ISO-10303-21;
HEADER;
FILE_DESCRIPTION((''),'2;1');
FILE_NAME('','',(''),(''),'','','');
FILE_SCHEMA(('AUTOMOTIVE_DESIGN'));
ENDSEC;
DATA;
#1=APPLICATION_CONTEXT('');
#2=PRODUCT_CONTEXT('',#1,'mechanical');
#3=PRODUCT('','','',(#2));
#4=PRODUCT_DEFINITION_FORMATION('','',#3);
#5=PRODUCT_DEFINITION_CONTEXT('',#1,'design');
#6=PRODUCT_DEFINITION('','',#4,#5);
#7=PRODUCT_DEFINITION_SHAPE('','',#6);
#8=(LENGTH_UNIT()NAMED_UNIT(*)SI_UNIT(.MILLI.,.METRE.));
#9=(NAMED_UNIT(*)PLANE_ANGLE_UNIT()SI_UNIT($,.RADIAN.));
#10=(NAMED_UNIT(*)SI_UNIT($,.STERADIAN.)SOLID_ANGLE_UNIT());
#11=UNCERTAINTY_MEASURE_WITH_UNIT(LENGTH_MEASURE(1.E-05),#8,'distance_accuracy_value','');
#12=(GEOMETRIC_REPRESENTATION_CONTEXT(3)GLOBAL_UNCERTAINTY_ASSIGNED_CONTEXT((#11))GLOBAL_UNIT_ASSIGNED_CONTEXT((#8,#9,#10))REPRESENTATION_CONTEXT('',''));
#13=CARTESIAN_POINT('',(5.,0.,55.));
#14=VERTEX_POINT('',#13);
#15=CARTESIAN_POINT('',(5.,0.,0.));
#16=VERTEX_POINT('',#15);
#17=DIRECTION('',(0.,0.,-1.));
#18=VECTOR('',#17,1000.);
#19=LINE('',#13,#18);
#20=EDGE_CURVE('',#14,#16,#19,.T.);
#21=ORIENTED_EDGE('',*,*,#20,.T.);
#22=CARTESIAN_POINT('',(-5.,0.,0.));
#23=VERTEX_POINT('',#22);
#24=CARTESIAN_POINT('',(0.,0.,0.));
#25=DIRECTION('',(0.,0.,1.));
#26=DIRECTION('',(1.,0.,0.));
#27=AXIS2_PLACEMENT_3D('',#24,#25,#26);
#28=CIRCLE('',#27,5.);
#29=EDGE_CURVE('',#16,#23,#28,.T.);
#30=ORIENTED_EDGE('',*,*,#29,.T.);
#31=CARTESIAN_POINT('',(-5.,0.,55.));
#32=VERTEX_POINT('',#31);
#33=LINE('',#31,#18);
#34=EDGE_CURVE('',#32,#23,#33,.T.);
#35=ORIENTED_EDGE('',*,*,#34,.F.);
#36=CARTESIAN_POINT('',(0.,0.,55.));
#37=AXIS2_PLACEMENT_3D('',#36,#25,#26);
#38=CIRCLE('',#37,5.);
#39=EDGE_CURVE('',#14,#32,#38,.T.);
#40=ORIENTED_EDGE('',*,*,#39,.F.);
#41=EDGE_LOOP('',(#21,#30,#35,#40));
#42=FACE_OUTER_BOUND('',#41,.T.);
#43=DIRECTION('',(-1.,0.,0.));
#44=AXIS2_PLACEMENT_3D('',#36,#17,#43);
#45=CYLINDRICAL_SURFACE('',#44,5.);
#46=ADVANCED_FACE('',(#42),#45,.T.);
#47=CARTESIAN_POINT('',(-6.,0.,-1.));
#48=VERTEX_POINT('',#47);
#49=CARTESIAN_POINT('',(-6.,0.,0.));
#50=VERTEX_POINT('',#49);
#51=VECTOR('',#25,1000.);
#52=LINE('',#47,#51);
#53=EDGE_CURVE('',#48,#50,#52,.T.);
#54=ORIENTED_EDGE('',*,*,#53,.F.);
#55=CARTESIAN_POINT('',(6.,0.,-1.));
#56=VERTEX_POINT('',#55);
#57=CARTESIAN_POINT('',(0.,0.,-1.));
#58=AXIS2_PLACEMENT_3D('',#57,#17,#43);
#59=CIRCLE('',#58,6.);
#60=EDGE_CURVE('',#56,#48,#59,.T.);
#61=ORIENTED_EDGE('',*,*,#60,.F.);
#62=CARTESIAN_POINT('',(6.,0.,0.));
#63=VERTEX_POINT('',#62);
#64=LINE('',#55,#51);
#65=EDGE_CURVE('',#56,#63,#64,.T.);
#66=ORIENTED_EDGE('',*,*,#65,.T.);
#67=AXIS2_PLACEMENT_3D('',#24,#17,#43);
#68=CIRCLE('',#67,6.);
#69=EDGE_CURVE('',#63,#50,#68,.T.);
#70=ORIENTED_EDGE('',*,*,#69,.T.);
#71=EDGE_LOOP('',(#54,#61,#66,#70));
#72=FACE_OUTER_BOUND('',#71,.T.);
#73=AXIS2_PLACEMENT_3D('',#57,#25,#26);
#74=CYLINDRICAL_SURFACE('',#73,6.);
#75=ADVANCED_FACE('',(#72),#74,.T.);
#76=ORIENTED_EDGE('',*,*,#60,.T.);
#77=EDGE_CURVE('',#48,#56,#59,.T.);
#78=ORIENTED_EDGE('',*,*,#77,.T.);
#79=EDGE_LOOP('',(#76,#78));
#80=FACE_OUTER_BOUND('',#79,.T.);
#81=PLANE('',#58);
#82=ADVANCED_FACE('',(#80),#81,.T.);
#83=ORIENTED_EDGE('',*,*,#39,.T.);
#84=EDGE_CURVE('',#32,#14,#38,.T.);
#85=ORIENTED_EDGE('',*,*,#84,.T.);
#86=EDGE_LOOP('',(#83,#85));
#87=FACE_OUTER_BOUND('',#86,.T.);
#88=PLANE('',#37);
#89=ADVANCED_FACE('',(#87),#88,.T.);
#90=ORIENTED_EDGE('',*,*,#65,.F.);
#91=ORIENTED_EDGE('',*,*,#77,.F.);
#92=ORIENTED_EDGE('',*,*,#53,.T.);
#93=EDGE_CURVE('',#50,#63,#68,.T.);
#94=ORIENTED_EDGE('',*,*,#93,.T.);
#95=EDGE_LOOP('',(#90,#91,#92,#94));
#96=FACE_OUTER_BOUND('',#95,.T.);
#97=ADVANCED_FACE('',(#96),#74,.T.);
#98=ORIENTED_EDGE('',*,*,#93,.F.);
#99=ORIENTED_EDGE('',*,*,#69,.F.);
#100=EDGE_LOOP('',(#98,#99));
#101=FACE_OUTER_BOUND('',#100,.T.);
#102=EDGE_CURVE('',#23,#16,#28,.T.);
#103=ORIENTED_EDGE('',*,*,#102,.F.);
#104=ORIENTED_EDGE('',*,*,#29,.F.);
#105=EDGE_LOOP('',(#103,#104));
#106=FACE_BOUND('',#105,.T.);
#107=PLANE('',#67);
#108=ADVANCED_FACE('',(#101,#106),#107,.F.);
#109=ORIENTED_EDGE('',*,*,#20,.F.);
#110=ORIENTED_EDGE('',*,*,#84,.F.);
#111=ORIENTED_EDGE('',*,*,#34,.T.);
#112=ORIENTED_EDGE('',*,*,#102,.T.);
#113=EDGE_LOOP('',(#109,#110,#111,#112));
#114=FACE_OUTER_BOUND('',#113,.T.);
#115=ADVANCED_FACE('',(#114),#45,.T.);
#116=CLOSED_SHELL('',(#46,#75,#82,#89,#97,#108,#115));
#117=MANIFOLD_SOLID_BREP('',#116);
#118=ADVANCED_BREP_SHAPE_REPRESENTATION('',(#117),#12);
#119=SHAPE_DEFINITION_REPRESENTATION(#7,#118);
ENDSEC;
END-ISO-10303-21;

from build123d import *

# Parameters (mm, degrees)
SKETCH_1_R      = 5
EXTRUDE_1_DEPTH = 55
SKETCH_2_R      = 6
EXTRUDE_2_DEPTH = 1


with BuildPart() as part:
    # 草图1 → 凸台-拉伸1 (new body)
    with BuildSketch(Plane.XY):
        Circle(SKETCH_1_R)
    extrude(amount=EXTRUDE_1_DEPTH)

    # 草图2 → 凸台-拉伸2 (add)
    with BuildSketch(Plane(origin=(0, 0, 0), x_dir=(-1, 0, 0), z_dir=(0, 0, -1))):
        Circle(SKETCH_2_R)
    extrude(amount=EXTRUDE_2_DEPTH)


solid = part.part
